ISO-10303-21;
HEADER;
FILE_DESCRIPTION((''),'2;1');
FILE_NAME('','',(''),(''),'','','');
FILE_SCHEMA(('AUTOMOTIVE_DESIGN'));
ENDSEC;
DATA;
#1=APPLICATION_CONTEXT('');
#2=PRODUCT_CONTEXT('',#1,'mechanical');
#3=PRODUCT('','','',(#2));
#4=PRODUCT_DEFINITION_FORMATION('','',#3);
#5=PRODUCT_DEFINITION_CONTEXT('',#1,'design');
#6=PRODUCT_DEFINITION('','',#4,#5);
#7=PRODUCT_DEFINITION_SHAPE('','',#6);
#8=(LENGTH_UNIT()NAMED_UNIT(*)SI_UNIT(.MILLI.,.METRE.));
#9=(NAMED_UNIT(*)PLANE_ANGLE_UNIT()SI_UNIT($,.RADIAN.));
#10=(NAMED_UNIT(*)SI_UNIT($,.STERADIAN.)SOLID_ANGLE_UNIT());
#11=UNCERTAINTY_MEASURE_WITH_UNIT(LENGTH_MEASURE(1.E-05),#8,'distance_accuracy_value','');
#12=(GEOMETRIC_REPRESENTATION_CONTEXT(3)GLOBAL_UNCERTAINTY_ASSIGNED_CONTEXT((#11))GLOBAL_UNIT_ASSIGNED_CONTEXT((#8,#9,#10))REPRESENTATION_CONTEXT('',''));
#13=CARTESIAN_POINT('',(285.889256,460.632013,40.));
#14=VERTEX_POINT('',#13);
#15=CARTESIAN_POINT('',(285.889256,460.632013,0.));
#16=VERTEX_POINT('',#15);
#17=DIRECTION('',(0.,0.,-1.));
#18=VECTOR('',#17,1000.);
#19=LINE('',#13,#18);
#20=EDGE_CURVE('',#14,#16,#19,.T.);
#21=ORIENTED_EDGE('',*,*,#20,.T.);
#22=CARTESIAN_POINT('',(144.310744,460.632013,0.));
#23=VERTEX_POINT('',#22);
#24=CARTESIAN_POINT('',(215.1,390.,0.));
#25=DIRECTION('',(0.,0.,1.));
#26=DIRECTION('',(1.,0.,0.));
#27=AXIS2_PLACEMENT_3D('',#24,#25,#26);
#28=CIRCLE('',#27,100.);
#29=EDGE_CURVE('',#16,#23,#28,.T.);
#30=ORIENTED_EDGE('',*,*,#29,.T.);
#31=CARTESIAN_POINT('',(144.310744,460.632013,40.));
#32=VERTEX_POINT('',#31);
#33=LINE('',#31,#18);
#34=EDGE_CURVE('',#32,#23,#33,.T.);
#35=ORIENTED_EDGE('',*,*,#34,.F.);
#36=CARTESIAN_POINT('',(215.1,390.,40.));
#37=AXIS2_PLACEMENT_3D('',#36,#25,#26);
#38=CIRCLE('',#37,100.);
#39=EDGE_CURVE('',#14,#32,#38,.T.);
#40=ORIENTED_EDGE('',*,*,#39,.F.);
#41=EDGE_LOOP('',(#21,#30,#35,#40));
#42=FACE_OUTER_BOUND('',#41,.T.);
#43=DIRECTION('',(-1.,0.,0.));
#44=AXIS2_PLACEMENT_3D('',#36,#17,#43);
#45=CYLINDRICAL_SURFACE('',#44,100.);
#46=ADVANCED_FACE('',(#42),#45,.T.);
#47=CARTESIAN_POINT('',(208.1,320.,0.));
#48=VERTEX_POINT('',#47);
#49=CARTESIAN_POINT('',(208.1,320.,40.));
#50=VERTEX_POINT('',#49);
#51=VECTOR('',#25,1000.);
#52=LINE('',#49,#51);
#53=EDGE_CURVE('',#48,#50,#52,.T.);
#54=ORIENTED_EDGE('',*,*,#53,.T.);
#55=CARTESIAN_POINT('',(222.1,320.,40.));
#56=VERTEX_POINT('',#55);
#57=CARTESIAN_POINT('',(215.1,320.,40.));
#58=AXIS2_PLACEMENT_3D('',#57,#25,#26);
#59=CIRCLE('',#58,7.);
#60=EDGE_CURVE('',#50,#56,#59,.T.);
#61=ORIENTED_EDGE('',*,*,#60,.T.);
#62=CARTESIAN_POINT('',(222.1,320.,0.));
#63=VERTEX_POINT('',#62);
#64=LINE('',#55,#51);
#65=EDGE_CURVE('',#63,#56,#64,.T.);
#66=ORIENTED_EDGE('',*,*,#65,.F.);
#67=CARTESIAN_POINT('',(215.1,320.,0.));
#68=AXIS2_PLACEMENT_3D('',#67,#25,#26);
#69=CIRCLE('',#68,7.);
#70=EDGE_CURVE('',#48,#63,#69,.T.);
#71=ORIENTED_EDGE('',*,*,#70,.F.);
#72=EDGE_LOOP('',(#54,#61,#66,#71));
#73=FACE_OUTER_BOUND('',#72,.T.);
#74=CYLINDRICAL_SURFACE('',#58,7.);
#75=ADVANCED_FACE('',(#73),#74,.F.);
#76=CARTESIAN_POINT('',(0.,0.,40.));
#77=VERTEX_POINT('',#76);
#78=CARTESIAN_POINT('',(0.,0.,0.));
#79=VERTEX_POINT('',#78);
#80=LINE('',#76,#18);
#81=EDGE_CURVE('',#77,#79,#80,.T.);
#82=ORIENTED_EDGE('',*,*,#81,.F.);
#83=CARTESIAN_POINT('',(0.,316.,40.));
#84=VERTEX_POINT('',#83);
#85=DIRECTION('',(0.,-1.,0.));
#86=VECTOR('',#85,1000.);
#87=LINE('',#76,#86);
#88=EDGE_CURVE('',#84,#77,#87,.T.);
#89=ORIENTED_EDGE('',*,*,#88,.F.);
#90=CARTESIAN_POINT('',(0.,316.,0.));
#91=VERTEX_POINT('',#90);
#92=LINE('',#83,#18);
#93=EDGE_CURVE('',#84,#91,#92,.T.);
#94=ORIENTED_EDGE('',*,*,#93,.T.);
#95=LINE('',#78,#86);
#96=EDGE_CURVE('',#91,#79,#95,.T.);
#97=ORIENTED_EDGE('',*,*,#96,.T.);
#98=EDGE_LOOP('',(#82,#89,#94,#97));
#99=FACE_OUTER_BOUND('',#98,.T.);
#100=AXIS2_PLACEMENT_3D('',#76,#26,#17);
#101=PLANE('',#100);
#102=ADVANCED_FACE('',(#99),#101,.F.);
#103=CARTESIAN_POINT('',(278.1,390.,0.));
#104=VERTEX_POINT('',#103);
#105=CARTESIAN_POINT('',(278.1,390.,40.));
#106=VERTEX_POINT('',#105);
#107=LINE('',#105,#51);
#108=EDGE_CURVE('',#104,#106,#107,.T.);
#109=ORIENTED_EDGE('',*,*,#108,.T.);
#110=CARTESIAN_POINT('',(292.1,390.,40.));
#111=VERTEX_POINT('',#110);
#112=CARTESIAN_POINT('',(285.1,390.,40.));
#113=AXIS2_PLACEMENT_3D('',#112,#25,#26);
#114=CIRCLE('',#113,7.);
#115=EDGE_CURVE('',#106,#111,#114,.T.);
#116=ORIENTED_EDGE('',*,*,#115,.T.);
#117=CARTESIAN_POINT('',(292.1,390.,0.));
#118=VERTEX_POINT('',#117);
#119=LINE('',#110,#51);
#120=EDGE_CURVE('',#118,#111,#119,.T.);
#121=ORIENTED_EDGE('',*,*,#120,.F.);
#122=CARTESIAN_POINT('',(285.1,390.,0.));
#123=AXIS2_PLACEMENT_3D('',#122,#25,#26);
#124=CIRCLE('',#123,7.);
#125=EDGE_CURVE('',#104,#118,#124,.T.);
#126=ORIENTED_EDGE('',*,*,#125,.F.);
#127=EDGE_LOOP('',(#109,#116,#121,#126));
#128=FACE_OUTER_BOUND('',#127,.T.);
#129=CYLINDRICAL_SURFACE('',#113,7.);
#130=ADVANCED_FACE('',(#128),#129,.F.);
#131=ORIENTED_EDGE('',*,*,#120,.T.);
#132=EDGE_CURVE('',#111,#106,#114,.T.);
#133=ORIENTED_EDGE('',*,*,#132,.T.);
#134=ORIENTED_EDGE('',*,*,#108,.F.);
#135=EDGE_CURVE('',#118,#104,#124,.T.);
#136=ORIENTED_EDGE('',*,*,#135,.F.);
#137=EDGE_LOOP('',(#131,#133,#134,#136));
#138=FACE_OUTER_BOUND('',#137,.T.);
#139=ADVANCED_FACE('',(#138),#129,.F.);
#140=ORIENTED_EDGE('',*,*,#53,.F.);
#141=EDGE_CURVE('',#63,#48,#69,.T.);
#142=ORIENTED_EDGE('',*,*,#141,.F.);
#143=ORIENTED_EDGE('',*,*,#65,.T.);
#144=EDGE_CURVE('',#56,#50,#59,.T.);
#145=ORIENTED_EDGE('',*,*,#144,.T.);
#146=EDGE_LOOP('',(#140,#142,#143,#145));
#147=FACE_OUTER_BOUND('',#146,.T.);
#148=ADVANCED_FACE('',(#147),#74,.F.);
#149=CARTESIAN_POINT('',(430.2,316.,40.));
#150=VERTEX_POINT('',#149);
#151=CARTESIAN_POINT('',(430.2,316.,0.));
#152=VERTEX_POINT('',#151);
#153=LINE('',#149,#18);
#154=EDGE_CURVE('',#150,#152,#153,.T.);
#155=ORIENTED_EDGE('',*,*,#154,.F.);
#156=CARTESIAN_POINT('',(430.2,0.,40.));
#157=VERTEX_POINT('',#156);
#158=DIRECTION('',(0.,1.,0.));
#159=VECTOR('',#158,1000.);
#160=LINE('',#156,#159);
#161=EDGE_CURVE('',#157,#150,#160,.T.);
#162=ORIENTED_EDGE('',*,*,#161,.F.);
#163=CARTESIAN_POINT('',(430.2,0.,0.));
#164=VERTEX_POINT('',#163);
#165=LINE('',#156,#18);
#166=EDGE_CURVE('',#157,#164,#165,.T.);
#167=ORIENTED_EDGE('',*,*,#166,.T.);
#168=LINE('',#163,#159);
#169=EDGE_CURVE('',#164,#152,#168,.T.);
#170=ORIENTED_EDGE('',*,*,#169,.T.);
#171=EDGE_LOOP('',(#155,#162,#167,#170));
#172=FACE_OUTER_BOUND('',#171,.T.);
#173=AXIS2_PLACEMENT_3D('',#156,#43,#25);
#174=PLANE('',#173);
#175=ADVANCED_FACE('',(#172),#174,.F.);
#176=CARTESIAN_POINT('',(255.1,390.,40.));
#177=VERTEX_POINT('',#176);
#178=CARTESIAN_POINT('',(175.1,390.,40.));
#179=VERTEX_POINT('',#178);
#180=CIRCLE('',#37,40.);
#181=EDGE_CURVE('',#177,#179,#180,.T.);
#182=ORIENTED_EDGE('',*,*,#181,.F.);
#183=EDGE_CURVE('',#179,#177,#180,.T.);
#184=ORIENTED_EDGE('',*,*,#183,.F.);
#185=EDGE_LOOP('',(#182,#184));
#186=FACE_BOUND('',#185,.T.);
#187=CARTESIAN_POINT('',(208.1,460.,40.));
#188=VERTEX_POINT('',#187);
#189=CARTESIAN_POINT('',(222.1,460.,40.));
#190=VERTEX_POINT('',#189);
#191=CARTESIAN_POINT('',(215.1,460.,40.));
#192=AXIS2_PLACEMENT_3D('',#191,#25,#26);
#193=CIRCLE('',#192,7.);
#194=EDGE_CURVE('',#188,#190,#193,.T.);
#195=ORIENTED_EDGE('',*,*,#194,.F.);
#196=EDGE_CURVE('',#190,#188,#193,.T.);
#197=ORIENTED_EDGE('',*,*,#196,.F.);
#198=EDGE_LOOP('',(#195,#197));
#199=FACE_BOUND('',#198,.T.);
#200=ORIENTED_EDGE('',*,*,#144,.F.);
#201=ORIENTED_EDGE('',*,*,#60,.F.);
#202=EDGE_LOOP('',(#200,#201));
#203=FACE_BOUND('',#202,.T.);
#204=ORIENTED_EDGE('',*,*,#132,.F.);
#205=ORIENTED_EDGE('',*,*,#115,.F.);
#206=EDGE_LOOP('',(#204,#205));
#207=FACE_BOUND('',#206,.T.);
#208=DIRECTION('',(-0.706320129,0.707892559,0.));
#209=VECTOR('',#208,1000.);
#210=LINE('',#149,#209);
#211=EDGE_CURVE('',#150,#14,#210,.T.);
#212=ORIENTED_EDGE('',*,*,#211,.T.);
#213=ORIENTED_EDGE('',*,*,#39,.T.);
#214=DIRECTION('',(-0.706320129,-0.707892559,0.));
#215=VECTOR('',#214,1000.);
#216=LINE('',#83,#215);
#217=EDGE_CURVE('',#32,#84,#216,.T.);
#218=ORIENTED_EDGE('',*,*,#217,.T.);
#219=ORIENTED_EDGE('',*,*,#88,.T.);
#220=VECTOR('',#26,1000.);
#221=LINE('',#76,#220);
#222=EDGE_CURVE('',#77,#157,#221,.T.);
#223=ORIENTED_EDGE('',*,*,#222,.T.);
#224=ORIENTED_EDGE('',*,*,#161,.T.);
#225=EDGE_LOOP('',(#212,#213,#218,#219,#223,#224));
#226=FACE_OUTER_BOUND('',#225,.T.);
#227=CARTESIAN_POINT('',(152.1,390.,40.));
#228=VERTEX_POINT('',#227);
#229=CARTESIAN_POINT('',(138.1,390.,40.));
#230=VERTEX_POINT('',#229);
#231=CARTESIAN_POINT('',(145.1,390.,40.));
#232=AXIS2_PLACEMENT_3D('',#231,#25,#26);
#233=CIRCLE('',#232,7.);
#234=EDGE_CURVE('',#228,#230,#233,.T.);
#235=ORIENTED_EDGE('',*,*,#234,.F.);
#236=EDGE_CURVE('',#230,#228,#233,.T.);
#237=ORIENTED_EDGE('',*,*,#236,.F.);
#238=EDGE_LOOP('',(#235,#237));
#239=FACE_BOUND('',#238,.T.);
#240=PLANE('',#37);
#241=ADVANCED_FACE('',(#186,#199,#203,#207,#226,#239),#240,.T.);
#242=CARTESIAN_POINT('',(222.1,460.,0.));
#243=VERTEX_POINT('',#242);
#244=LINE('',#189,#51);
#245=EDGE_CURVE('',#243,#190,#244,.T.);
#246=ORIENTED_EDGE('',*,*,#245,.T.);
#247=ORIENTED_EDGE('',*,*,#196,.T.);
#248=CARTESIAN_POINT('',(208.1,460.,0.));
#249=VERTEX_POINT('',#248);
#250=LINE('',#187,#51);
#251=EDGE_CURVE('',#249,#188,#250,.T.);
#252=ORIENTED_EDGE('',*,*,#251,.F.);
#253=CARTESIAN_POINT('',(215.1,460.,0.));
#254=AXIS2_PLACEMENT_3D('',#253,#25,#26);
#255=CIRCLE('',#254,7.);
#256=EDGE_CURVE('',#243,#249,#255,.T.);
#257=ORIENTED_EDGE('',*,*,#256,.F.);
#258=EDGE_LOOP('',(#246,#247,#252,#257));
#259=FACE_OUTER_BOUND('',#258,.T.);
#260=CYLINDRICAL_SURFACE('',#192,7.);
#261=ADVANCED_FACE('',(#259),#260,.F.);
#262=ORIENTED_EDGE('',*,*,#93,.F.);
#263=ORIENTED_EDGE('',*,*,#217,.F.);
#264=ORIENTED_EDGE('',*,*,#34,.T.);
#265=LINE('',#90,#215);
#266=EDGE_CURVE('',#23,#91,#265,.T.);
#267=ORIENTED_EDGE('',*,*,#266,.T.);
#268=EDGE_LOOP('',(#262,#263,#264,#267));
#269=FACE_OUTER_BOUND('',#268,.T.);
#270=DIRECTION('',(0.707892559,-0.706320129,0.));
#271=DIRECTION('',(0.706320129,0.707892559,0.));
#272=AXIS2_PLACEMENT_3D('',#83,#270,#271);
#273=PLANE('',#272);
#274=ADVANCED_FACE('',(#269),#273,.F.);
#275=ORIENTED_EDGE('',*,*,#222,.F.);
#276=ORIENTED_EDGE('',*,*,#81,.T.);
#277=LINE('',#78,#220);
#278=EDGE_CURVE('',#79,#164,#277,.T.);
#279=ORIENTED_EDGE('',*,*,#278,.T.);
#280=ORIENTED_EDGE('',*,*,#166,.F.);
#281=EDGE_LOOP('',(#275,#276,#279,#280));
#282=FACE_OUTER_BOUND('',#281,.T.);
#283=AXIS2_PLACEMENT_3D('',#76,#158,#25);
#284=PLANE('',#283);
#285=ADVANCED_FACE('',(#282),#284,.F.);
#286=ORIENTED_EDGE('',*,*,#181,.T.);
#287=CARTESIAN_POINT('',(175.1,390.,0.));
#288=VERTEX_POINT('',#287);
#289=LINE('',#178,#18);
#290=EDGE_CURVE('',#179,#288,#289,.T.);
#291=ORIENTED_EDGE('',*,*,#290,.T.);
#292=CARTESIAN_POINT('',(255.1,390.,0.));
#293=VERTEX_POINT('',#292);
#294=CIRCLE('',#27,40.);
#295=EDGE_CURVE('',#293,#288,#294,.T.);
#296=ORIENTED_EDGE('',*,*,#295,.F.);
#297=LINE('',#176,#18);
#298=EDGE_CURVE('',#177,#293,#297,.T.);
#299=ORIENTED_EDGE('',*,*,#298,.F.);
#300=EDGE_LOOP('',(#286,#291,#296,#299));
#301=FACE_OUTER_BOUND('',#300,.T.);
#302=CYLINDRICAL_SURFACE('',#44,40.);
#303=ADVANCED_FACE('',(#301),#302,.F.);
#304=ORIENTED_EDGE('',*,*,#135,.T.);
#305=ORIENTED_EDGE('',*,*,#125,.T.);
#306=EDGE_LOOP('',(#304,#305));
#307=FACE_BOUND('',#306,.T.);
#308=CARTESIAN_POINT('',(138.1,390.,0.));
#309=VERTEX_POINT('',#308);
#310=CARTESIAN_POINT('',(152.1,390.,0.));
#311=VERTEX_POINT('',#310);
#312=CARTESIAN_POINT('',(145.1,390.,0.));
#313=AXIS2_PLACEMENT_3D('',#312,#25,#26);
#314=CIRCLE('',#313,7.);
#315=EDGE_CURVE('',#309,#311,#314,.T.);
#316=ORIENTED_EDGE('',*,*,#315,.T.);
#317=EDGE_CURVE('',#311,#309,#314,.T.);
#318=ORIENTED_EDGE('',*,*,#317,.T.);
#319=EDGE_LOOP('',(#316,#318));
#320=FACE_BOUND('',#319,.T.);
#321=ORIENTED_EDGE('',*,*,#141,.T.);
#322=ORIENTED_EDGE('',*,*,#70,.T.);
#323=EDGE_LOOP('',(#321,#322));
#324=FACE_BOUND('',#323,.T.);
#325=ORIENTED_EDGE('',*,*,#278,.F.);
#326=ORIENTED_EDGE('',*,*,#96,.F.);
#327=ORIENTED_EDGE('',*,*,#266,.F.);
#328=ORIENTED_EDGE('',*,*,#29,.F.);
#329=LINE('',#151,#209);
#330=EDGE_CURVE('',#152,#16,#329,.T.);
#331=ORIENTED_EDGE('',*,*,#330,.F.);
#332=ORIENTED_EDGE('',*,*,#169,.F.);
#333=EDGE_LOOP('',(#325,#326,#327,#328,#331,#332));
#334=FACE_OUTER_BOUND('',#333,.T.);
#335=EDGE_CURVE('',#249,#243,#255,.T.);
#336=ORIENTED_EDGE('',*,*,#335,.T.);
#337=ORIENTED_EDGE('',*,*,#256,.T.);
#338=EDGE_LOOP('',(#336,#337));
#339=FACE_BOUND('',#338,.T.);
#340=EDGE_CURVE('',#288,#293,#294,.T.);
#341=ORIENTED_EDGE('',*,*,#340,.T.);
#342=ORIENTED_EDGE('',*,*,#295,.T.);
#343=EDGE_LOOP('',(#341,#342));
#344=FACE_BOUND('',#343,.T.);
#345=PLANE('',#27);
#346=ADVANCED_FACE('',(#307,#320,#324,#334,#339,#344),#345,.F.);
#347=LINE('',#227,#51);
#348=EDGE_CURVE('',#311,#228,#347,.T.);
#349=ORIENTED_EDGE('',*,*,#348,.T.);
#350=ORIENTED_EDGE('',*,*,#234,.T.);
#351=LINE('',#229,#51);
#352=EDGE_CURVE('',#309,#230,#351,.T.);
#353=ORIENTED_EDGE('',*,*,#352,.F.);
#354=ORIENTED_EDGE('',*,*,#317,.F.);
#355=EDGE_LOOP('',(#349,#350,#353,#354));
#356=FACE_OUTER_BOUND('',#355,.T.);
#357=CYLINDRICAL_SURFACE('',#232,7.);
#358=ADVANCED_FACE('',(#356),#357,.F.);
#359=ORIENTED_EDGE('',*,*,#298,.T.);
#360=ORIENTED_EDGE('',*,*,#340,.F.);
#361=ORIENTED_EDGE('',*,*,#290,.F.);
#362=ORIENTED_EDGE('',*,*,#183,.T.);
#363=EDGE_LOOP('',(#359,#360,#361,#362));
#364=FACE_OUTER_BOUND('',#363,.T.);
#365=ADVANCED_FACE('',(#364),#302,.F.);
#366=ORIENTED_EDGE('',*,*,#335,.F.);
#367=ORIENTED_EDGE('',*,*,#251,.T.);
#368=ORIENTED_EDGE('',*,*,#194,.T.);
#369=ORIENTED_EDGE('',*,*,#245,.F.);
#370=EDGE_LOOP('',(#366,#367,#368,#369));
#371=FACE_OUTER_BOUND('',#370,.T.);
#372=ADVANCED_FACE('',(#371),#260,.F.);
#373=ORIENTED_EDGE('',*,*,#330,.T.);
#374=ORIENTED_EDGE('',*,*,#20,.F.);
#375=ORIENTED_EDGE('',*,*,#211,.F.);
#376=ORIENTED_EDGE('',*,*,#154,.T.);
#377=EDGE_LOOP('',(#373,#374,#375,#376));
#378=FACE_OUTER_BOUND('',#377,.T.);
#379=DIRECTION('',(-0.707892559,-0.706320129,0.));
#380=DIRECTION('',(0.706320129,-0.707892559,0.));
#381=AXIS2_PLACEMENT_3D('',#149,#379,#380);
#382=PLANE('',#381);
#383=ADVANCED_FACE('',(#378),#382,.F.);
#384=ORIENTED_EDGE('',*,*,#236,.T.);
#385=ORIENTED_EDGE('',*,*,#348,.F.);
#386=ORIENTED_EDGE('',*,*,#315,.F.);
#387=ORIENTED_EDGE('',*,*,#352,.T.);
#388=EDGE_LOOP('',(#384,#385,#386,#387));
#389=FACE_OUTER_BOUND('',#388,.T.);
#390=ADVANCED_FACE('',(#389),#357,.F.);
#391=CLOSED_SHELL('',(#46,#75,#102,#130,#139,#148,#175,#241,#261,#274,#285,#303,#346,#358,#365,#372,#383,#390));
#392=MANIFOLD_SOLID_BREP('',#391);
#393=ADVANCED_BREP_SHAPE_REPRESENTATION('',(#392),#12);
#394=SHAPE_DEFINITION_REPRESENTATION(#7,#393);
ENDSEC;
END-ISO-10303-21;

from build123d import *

# Parameters (mm, degrees)
SKETCH1_R           = 40
BOSS_EXTRUDE1_DEPTH = 40
M16_TAPPED_HOLE1_D  = 14


with BuildPart() as part:
    # Sketch1 → Boss-Extrude1 (new body)
    with BuildSketch(Plane.XY):
        with BuildLine():
            Line((0, 0), (430.2, 0))
            Line((430.2, 0), (430.2, 316))
            Line((430.2, 316), (285.889255941, 460.632012878))
            ThreePointArc((285.889255941, 460.632012878), (215.1, 490), (144.310744059, 460.632012878))
            Line((144.310744059, 460.632012878), (0, 316))
            Line((0, 316), (0, 0))
        make_face()
        with Locations((215.1, 390)):
            Circle(SKETCH1_R, mode=Mode.SUBTRACT)
    extrude(amount=BOSS_EXTRUDE1_DEPTH)

    # M16 Tapped Hole1 (through all)
    with Locations(Plane.XY.offset(40)):
        with Locations((215.1, 460), (285.1, 390), (215.1, 320), (145.1, 390)):
            Hole(M16_TAPPED_HOLE1_D / 2)


solid = part.part
